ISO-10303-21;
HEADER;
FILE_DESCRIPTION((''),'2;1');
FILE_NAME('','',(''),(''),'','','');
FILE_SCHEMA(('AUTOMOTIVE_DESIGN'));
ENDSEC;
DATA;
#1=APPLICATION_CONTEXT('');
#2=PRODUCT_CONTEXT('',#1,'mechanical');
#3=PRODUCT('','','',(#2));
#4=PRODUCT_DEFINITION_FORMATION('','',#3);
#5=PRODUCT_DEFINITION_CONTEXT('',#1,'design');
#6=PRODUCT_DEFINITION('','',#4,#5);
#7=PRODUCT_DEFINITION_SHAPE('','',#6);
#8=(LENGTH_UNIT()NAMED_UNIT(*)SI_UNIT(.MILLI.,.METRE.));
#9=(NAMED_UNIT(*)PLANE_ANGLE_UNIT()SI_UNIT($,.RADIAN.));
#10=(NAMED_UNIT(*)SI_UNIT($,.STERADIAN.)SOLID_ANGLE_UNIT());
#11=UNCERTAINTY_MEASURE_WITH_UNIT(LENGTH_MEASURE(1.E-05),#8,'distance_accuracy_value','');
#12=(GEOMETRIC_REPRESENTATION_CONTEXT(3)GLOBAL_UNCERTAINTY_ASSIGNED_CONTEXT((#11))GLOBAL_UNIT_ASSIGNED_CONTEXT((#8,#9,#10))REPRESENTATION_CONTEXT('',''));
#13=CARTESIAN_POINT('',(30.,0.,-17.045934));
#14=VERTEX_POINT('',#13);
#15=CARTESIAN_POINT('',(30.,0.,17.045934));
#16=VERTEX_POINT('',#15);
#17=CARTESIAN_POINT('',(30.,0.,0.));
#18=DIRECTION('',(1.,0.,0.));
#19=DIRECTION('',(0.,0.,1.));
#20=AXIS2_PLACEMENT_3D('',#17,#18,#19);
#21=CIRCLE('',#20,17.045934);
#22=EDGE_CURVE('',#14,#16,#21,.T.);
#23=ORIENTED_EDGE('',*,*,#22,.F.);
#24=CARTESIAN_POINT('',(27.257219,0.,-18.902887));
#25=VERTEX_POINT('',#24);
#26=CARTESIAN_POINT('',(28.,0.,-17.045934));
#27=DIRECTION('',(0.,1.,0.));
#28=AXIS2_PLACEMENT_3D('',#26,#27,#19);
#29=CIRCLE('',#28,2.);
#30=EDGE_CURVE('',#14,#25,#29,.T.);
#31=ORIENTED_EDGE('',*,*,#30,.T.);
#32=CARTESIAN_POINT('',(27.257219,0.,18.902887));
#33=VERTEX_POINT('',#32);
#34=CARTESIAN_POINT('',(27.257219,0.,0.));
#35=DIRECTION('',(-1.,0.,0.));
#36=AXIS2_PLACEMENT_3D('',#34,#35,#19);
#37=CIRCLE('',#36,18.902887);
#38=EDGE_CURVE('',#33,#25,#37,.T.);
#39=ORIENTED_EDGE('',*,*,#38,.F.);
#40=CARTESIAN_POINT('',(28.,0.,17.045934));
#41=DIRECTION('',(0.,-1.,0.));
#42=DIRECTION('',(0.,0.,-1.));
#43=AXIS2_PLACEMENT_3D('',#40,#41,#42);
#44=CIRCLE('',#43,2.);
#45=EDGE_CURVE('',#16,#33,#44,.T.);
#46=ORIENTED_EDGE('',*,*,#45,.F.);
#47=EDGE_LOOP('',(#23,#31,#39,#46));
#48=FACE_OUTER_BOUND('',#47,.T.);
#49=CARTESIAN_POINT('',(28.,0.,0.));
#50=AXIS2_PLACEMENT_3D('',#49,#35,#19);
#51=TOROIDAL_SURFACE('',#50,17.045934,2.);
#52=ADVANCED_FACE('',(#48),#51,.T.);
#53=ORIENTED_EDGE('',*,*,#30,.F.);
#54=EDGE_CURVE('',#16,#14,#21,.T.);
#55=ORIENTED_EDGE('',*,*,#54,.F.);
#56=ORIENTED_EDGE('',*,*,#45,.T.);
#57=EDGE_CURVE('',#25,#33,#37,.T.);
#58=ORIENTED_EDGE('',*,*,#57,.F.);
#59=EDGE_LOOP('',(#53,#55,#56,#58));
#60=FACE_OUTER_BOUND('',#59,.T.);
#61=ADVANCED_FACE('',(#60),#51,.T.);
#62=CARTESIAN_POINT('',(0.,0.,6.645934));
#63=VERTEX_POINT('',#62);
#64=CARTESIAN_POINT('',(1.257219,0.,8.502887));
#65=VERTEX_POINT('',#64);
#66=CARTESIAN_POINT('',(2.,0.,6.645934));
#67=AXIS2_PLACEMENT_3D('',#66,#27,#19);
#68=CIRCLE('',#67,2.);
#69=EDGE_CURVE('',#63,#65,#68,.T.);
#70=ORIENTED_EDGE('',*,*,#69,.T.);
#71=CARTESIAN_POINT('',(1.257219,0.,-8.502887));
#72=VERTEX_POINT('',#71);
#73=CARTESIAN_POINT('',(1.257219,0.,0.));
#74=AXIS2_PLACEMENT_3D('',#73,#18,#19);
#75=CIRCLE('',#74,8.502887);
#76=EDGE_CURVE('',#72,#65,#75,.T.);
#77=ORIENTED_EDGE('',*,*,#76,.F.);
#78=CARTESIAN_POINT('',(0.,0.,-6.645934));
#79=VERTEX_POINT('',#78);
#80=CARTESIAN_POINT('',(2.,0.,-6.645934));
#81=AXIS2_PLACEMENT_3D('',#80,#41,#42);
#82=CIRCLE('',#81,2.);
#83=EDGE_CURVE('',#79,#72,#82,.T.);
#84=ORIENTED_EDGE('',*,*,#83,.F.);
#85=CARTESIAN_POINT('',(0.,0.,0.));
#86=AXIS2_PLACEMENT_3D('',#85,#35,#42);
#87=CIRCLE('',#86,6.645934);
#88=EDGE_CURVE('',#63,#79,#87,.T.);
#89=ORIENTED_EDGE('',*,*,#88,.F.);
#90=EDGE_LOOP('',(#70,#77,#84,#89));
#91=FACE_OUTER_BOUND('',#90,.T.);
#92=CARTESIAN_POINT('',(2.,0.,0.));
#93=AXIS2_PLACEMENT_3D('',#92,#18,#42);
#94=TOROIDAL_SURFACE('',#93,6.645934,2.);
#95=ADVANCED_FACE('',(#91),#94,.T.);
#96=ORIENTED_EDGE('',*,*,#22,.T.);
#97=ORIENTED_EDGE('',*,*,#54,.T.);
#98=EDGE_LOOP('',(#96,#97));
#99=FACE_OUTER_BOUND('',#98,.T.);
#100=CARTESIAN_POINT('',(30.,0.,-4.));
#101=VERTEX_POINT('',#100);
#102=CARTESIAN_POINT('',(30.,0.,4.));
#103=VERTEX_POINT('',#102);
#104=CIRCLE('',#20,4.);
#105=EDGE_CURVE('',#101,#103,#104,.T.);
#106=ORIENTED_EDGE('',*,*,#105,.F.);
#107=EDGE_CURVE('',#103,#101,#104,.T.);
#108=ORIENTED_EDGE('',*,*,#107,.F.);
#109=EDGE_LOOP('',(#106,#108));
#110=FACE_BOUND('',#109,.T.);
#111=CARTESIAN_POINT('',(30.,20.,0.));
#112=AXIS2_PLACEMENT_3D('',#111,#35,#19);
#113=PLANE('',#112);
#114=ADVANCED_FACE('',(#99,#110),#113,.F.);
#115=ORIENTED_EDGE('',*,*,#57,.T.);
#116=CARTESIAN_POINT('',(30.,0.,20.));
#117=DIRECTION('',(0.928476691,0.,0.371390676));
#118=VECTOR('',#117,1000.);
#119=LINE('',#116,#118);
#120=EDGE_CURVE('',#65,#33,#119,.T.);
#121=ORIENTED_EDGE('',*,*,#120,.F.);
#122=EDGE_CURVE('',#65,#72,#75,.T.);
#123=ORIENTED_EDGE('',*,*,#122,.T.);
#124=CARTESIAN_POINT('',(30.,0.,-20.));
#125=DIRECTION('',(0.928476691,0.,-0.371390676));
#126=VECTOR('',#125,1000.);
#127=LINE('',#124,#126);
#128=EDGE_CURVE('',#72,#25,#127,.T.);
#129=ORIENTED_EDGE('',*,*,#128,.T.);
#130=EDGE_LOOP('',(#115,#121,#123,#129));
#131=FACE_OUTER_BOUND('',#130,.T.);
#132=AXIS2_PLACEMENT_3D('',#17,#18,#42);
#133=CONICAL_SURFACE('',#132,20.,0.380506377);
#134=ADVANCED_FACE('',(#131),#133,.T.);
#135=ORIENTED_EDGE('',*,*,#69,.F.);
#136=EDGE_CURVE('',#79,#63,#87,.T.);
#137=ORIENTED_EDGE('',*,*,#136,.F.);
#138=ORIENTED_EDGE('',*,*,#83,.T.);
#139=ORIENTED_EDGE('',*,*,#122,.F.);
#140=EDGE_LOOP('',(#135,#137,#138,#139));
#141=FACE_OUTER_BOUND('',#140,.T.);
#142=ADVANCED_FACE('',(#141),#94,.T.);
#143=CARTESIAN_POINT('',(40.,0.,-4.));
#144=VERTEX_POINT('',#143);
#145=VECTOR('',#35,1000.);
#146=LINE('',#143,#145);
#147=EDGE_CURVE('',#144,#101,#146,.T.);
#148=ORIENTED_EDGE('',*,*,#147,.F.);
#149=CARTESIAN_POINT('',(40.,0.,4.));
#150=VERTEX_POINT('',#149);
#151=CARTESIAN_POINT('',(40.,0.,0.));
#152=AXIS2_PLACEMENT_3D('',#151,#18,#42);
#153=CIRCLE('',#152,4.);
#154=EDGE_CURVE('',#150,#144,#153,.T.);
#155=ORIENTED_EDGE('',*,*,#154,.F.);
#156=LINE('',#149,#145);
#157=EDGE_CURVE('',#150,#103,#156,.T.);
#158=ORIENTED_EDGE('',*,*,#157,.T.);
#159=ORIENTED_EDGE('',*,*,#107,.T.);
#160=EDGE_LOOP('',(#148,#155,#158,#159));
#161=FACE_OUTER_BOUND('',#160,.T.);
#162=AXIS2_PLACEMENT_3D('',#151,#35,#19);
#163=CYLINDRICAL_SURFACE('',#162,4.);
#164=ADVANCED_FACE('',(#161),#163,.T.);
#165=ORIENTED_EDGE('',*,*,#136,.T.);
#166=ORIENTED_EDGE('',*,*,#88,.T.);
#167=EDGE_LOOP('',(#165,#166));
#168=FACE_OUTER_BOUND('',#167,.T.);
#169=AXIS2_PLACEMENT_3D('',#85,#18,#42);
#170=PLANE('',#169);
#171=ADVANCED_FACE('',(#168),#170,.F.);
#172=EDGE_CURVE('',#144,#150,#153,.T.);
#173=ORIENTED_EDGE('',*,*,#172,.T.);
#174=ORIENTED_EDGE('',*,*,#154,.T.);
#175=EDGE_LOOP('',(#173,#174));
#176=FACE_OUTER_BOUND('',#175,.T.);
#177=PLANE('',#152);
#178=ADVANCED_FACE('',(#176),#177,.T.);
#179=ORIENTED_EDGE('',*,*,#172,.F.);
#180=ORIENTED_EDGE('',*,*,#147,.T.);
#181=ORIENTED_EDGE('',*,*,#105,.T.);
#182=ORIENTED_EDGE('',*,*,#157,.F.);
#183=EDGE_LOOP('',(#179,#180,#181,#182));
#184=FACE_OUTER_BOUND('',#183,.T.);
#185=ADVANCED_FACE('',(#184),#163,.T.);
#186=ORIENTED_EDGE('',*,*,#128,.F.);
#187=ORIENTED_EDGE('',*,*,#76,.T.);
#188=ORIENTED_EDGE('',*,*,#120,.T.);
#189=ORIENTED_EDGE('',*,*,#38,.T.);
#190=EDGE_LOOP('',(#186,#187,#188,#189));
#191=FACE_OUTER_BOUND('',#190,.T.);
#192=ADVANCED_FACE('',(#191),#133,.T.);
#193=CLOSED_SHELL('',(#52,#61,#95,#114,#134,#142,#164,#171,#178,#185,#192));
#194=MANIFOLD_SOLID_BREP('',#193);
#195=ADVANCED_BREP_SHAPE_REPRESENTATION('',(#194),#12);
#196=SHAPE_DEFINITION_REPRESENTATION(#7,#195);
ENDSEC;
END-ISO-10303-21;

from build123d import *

# Parameters (mm, degrees)
FILLET1_R           = 2
SKETCH2_R           = 4
BOSS_EXTRUDE1_DEPTH = 10
FILLET2_R           = 2


with BuildPart() as part:
    # Sketch1 → Revolve1 (revolve)
    with BuildSketch(Plane.XY, mode=Mode.PRIVATE) as revolve1_sk:
        Polygon((30, 20), (30, 0), (0, 0), (0, 8), align=None)
    revolve(revolve1_sk.sketch.rotate(Axis((10.657678515, 0, 0), (1, 0, 0)), 90), axis=Axis((10.657678515, 0, 0), (1, 0, 0)))

    # Fillet1
    fillet1_edges = [part.edges().sort_by_distance(p)[0] for p in [
        (0, 0, -8),
    ]]
    fillet(fillet1_edges, radius=FILLET1_R)

    # Sketch2 → Boss-Extrude1 (add)
    with BuildSketch(Plane(origin=(30, 0, 0), x_dir=(0, 0, -1), z_dir=(1, 0, 0))):
        with Locations(Location((0, 0, 0), (0, 0, 180))):
            Circle(SKETCH2_R)
    extrude(amount=BOSS_EXTRUDE1_DEPTH)

    # Fillet2
    fillet2_edges = [part.edges().sort_by_distance(p)[0] for p in [
        (30, 0, -20),
    ]]
    fillet(fillet2_edges, radius=FILLET2_R)


solid = part.part
